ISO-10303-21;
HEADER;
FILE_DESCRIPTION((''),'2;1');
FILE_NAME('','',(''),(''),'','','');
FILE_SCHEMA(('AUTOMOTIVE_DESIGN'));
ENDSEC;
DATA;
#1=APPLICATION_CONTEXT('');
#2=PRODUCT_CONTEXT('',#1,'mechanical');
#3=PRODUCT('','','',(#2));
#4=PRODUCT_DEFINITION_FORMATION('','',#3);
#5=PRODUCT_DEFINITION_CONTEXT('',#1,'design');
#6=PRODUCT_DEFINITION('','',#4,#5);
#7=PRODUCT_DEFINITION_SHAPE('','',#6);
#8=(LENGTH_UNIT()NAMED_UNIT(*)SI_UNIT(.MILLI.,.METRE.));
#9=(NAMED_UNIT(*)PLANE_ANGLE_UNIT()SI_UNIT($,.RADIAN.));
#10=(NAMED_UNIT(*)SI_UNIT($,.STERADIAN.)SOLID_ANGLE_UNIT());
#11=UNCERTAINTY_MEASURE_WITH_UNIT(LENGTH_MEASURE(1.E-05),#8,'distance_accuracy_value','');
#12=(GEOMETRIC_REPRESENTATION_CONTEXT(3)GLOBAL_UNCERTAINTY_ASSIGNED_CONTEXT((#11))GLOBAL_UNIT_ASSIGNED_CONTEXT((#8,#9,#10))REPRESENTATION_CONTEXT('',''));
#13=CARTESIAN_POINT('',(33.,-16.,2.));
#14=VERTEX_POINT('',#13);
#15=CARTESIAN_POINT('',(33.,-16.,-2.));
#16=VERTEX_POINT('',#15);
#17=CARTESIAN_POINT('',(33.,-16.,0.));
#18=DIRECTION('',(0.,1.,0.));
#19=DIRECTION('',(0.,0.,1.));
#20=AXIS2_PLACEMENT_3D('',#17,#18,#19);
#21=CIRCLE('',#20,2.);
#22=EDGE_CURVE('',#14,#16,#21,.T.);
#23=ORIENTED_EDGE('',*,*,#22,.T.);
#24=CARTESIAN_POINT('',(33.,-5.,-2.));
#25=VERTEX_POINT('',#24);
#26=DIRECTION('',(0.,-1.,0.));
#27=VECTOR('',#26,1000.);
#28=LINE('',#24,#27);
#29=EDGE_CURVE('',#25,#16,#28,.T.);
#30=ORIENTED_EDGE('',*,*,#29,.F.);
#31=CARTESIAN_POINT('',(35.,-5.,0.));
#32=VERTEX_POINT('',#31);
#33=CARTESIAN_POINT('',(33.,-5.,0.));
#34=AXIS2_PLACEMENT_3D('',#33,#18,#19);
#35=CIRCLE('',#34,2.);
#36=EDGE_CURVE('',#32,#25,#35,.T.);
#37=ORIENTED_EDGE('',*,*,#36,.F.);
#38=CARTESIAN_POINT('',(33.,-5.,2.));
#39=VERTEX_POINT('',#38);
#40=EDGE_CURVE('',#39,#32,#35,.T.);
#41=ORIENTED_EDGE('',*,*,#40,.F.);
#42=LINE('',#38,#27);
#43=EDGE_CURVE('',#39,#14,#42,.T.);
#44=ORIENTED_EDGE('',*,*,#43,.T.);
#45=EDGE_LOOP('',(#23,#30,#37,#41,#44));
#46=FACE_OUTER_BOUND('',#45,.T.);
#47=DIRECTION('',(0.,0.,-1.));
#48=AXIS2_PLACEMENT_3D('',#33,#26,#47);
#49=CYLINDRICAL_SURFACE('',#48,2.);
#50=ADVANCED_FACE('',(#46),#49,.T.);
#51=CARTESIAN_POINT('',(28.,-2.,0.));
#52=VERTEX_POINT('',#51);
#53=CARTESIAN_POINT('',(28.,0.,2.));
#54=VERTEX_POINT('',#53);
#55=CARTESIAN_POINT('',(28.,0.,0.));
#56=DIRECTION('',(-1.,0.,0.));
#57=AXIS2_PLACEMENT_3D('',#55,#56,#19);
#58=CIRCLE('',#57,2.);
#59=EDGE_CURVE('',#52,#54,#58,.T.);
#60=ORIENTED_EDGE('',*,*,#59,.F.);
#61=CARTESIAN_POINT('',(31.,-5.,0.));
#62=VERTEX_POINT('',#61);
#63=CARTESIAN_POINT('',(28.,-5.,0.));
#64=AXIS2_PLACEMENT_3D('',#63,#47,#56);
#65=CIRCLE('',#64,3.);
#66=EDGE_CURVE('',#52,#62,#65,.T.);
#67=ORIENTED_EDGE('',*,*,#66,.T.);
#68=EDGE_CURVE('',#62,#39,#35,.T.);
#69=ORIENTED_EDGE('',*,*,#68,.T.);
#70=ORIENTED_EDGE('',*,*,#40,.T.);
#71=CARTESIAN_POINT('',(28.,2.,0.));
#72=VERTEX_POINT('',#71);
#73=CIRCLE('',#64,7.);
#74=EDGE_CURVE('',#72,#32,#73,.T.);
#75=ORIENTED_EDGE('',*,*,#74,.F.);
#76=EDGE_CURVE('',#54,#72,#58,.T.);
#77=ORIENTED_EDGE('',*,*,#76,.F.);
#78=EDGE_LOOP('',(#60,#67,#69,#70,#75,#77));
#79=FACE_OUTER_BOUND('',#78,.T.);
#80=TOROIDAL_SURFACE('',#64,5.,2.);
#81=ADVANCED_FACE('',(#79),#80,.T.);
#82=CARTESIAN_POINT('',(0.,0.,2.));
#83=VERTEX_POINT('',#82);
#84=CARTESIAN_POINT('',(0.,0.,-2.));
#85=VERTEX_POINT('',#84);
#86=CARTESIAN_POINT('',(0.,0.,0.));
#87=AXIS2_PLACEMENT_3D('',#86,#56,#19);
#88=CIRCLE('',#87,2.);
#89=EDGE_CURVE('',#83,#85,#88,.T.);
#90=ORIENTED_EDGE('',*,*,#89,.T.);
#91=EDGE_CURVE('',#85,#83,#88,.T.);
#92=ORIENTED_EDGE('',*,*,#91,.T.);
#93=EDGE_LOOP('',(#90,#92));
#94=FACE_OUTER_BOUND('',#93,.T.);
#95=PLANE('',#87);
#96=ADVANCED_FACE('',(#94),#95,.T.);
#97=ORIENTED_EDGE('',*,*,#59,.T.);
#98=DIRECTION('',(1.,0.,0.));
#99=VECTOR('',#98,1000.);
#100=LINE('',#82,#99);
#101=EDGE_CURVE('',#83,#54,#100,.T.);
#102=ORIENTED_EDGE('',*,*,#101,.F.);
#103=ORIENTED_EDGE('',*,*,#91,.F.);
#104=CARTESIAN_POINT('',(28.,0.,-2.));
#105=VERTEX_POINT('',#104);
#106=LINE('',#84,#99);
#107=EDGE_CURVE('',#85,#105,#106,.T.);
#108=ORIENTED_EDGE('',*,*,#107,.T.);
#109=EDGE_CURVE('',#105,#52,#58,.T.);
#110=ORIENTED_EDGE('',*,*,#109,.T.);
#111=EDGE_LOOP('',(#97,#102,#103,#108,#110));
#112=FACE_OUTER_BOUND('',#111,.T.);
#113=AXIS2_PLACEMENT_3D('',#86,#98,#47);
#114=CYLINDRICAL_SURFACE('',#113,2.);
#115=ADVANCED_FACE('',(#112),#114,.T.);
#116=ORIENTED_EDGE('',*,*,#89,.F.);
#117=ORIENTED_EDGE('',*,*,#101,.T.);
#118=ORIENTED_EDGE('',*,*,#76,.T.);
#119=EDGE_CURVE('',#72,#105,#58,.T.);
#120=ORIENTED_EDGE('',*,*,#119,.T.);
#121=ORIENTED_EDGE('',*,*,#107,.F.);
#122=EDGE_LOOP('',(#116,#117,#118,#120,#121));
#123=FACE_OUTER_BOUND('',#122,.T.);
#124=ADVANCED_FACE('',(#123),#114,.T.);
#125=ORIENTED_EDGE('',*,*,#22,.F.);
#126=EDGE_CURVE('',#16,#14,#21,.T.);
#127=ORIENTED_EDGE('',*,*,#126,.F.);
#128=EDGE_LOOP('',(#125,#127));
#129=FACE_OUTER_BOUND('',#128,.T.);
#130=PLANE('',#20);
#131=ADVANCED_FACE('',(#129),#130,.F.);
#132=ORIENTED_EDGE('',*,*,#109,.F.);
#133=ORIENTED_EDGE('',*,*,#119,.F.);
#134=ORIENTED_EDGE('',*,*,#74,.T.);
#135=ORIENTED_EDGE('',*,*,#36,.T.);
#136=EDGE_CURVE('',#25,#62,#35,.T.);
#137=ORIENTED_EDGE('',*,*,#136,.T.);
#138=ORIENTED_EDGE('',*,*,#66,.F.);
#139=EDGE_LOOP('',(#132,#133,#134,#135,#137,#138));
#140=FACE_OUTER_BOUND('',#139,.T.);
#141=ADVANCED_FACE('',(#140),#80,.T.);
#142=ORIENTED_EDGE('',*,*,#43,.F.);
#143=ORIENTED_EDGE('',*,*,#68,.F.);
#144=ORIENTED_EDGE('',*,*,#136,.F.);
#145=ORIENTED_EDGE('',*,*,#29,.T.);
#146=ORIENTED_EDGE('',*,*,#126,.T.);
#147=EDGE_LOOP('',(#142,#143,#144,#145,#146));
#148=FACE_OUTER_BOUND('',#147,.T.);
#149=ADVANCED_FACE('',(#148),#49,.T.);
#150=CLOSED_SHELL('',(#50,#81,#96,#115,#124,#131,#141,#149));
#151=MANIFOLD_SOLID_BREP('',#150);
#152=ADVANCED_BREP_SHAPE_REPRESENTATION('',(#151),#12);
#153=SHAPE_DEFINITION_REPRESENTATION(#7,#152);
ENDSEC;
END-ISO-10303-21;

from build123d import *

# Parameters (mm, degrees)
SWEEP1_PROFILE_R = 2


with BuildPart() as part:
    # Sweep1: sweep along a path in Sketch1
    with BuildLine(Plane.XY) as sweep1_path:
        Line((0, 0), (28, 0))
        ThreePointArc((28, 0), (31.535533906, -1.464466094), (33, -5))
        Line((33, -5), (33, -16))
    # Sweep1 profile (on start of the path) → Sweep1 (sweep)
    with BuildSketch(Plane(origin=(0, 0, 0), x_dir=(0, 0, 1), z_dir=(1, 0, 0))):
        Circle(SWEEP1_PROFILE_R)
    sweep(path=sweep1_path.line)


solid = part.part
